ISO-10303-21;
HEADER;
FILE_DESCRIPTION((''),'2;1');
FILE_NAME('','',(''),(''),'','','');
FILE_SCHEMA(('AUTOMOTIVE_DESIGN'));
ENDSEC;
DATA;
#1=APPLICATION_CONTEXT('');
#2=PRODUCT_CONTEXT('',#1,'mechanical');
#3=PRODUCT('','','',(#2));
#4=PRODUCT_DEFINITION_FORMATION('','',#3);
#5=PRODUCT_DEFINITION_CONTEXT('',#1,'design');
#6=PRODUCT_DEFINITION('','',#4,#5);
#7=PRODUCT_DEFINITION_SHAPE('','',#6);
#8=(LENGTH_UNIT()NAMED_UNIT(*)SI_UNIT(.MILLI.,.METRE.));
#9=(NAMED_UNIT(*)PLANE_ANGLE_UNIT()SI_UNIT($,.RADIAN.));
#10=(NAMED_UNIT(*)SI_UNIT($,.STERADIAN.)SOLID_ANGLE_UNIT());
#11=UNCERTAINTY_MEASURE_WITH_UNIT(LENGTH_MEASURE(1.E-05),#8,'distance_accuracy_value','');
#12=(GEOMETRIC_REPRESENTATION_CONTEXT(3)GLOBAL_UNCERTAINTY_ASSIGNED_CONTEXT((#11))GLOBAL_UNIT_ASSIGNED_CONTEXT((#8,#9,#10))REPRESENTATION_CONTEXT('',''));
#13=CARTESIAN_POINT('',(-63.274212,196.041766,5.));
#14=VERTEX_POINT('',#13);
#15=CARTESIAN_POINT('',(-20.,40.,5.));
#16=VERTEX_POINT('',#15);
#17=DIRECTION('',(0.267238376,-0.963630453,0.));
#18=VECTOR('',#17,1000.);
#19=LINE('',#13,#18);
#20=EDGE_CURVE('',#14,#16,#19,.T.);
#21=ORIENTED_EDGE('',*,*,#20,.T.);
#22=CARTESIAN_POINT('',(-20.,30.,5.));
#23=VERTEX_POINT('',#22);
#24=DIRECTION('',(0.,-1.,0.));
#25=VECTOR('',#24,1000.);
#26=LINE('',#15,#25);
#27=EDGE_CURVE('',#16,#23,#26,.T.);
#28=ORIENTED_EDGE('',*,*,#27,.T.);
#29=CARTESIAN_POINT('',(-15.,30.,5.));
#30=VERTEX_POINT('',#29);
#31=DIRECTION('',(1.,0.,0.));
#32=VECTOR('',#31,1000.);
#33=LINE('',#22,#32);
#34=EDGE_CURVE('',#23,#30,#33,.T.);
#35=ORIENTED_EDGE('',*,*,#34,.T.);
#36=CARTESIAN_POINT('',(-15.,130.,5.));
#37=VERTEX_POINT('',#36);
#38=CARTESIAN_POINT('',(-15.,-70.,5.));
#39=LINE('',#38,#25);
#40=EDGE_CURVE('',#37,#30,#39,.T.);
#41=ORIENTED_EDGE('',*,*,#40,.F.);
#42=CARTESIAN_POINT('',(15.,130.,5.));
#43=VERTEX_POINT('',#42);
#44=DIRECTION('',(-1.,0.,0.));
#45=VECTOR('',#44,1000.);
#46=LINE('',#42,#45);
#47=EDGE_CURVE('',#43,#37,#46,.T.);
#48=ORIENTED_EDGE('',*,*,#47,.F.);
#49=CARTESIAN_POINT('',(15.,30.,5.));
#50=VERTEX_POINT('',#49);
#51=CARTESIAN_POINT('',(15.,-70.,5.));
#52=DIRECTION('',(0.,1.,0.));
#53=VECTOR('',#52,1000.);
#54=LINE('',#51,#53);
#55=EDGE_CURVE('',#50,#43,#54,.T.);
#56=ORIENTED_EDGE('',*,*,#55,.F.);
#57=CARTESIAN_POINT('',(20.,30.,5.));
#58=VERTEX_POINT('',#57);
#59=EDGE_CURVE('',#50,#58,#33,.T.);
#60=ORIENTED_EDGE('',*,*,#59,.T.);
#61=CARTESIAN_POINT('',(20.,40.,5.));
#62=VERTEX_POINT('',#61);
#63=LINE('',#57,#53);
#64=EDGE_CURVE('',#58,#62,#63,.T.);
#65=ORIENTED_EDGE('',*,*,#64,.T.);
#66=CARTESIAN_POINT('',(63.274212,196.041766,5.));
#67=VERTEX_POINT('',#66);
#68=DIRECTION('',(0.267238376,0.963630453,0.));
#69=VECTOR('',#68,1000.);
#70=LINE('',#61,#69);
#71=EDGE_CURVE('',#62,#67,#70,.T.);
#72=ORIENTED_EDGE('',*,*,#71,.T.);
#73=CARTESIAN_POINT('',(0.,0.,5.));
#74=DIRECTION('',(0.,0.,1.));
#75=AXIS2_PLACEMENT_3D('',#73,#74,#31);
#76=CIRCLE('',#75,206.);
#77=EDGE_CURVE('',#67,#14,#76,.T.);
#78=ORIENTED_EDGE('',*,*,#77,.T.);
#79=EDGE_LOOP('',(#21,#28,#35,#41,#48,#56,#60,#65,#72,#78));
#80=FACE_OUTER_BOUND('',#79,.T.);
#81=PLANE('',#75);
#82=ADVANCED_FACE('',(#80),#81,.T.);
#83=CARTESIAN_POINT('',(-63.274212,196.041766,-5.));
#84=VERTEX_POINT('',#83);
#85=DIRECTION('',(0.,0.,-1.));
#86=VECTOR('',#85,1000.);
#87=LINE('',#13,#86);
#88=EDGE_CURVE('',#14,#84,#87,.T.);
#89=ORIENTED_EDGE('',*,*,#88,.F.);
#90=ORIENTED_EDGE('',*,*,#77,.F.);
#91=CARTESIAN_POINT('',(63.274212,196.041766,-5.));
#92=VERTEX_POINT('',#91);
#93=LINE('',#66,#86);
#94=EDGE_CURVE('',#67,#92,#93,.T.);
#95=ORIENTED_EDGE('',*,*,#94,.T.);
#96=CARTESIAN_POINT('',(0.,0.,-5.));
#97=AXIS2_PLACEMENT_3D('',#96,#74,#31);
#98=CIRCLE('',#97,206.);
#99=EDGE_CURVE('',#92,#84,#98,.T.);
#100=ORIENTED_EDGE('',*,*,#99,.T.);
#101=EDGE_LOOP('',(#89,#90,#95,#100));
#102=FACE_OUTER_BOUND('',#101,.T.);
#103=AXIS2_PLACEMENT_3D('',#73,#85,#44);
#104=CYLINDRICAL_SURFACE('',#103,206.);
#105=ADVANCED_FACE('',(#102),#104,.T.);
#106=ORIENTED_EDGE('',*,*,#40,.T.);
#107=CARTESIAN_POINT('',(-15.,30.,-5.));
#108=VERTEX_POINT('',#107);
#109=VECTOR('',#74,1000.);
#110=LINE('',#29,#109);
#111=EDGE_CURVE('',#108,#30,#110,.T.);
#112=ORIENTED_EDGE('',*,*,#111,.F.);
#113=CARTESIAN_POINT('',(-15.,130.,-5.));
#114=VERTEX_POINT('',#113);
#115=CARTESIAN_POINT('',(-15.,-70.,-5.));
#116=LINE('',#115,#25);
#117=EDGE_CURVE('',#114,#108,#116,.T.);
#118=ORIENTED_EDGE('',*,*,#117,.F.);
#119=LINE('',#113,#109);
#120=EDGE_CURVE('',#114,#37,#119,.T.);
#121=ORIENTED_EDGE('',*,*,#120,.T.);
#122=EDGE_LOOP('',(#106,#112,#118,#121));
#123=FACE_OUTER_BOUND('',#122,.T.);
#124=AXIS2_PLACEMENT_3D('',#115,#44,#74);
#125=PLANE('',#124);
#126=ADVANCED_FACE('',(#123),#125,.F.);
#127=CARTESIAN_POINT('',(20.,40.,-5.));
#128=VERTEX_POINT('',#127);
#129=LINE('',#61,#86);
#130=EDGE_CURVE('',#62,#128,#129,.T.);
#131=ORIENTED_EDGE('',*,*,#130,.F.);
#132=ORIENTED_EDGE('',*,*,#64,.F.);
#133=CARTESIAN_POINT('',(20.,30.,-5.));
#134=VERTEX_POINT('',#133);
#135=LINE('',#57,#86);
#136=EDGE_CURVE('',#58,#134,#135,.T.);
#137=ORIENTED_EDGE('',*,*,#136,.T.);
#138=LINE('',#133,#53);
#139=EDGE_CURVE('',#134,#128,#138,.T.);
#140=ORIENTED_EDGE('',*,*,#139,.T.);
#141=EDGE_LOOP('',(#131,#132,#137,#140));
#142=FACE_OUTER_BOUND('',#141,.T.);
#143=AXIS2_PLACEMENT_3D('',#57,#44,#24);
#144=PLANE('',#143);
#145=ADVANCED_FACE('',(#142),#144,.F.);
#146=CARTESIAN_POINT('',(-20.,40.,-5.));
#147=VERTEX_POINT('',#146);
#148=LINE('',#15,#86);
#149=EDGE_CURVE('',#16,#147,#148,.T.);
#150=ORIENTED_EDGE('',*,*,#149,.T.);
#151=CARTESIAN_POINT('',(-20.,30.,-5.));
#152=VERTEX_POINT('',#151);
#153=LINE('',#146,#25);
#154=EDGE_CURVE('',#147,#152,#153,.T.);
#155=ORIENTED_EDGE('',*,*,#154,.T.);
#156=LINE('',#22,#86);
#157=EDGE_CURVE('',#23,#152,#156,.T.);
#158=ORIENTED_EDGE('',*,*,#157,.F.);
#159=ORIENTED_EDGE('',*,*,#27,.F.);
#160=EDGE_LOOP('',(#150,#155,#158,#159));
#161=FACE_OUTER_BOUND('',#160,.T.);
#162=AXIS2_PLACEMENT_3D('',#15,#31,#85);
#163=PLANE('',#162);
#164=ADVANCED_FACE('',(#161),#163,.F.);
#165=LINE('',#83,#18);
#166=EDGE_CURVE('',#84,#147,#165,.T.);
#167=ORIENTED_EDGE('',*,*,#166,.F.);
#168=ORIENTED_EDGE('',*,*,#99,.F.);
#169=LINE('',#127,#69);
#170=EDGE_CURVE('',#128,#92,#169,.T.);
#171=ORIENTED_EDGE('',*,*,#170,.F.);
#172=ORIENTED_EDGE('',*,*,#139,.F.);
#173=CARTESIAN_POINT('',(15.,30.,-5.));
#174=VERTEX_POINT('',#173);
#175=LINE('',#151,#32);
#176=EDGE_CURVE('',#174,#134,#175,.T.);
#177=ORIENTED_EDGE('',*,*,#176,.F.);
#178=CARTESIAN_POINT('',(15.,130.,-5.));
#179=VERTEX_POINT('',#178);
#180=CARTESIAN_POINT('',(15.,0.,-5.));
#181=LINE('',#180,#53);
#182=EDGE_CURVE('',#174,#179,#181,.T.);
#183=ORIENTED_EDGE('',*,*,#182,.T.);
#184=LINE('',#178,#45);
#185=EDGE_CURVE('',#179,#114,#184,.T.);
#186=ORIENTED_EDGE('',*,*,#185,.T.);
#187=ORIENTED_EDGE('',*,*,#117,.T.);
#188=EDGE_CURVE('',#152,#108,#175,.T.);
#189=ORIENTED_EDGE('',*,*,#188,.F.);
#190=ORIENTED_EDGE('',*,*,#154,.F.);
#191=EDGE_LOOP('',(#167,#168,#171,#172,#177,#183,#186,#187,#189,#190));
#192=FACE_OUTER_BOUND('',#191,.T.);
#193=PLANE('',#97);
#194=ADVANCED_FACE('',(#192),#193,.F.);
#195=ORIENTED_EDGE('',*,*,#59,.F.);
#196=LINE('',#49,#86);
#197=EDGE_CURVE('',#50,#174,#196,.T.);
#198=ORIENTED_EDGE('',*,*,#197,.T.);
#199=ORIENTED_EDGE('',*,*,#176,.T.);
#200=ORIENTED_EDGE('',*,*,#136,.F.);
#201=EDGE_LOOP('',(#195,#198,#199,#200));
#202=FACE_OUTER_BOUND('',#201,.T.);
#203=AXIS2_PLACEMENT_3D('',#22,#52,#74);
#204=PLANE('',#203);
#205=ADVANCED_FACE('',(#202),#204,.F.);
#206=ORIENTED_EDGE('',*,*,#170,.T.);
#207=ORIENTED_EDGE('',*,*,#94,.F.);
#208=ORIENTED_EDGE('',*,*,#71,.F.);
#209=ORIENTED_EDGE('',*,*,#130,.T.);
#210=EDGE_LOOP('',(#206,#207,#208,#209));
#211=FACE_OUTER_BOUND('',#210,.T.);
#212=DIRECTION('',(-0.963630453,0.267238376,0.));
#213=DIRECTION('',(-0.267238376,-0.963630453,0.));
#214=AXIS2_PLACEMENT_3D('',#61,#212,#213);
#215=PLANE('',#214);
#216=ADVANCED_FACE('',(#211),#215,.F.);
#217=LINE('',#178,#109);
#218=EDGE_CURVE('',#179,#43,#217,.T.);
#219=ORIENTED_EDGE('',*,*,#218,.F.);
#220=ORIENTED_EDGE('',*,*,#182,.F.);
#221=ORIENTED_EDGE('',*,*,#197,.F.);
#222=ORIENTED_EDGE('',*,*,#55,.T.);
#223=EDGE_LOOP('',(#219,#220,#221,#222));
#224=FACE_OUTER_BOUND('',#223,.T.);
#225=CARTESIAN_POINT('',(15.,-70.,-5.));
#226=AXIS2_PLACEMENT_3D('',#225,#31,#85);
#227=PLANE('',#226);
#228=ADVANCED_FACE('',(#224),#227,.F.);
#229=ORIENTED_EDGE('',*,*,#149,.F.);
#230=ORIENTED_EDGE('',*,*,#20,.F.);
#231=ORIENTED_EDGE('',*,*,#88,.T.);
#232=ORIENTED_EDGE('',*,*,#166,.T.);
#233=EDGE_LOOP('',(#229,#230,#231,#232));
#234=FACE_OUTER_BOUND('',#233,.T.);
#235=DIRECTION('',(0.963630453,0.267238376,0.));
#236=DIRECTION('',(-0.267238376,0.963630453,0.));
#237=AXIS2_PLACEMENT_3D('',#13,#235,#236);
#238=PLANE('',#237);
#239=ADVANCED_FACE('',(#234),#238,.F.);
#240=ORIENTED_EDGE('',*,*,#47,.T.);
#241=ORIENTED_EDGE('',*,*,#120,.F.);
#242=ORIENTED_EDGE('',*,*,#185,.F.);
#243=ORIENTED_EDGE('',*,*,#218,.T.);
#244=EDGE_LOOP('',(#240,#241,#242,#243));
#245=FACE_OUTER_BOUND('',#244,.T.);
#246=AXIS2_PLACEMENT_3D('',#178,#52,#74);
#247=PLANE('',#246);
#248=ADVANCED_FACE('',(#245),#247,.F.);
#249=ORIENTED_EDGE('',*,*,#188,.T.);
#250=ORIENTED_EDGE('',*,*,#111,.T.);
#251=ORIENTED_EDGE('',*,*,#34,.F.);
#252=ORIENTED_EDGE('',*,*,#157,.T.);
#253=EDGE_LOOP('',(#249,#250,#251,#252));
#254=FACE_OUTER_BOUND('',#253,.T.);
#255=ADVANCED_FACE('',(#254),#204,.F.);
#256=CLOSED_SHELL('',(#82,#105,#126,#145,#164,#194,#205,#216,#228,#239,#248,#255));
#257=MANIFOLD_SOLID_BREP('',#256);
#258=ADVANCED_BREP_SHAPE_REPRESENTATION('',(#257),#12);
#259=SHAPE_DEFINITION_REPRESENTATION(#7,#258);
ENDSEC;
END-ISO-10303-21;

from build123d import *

# Parameters (mm, degrees)
BOSS_EXTRUDE1_DEPTH = 5
SKETCH2_W           = 30
SKETCH2_H           = 200
CUT_EXTRUDE1_DEPTH  = 10


with BuildPart() as part:
    # Sketch1 → Boss-Extrude1 (new, symmetric)
    with BuildSketch(Plane.XY):
        with BuildLine():
            Line((-63.274211694, 196.041766301), (-20, 40))
            Line((-20, 40), (-20, 30))
            Line((-20, 30), (20, 30))
            Line((20, 30), (20, 40))
            Line((20, 40), (63.274211694, 196.041766301))
            ThreePointArc((63.274211694, 196.041766301), (0, 206), (-63.274211694, 196.041766301))
        make_face()
    extrude(amount=BOSS_EXTRUDE1_DEPTH, both=True)

    # Sketch2 → Cut-Extrude1 (cut)
    with BuildSketch(Plane.XY.offset(5)):
        with Locations((0, 30)):
            Rectangle(SKETCH2_W, SKETCH2_H)
    extrude(amount=-CUT_EXTRUDE1_DEPTH, mode=Mode.SUBTRACT)


solid = part.part
